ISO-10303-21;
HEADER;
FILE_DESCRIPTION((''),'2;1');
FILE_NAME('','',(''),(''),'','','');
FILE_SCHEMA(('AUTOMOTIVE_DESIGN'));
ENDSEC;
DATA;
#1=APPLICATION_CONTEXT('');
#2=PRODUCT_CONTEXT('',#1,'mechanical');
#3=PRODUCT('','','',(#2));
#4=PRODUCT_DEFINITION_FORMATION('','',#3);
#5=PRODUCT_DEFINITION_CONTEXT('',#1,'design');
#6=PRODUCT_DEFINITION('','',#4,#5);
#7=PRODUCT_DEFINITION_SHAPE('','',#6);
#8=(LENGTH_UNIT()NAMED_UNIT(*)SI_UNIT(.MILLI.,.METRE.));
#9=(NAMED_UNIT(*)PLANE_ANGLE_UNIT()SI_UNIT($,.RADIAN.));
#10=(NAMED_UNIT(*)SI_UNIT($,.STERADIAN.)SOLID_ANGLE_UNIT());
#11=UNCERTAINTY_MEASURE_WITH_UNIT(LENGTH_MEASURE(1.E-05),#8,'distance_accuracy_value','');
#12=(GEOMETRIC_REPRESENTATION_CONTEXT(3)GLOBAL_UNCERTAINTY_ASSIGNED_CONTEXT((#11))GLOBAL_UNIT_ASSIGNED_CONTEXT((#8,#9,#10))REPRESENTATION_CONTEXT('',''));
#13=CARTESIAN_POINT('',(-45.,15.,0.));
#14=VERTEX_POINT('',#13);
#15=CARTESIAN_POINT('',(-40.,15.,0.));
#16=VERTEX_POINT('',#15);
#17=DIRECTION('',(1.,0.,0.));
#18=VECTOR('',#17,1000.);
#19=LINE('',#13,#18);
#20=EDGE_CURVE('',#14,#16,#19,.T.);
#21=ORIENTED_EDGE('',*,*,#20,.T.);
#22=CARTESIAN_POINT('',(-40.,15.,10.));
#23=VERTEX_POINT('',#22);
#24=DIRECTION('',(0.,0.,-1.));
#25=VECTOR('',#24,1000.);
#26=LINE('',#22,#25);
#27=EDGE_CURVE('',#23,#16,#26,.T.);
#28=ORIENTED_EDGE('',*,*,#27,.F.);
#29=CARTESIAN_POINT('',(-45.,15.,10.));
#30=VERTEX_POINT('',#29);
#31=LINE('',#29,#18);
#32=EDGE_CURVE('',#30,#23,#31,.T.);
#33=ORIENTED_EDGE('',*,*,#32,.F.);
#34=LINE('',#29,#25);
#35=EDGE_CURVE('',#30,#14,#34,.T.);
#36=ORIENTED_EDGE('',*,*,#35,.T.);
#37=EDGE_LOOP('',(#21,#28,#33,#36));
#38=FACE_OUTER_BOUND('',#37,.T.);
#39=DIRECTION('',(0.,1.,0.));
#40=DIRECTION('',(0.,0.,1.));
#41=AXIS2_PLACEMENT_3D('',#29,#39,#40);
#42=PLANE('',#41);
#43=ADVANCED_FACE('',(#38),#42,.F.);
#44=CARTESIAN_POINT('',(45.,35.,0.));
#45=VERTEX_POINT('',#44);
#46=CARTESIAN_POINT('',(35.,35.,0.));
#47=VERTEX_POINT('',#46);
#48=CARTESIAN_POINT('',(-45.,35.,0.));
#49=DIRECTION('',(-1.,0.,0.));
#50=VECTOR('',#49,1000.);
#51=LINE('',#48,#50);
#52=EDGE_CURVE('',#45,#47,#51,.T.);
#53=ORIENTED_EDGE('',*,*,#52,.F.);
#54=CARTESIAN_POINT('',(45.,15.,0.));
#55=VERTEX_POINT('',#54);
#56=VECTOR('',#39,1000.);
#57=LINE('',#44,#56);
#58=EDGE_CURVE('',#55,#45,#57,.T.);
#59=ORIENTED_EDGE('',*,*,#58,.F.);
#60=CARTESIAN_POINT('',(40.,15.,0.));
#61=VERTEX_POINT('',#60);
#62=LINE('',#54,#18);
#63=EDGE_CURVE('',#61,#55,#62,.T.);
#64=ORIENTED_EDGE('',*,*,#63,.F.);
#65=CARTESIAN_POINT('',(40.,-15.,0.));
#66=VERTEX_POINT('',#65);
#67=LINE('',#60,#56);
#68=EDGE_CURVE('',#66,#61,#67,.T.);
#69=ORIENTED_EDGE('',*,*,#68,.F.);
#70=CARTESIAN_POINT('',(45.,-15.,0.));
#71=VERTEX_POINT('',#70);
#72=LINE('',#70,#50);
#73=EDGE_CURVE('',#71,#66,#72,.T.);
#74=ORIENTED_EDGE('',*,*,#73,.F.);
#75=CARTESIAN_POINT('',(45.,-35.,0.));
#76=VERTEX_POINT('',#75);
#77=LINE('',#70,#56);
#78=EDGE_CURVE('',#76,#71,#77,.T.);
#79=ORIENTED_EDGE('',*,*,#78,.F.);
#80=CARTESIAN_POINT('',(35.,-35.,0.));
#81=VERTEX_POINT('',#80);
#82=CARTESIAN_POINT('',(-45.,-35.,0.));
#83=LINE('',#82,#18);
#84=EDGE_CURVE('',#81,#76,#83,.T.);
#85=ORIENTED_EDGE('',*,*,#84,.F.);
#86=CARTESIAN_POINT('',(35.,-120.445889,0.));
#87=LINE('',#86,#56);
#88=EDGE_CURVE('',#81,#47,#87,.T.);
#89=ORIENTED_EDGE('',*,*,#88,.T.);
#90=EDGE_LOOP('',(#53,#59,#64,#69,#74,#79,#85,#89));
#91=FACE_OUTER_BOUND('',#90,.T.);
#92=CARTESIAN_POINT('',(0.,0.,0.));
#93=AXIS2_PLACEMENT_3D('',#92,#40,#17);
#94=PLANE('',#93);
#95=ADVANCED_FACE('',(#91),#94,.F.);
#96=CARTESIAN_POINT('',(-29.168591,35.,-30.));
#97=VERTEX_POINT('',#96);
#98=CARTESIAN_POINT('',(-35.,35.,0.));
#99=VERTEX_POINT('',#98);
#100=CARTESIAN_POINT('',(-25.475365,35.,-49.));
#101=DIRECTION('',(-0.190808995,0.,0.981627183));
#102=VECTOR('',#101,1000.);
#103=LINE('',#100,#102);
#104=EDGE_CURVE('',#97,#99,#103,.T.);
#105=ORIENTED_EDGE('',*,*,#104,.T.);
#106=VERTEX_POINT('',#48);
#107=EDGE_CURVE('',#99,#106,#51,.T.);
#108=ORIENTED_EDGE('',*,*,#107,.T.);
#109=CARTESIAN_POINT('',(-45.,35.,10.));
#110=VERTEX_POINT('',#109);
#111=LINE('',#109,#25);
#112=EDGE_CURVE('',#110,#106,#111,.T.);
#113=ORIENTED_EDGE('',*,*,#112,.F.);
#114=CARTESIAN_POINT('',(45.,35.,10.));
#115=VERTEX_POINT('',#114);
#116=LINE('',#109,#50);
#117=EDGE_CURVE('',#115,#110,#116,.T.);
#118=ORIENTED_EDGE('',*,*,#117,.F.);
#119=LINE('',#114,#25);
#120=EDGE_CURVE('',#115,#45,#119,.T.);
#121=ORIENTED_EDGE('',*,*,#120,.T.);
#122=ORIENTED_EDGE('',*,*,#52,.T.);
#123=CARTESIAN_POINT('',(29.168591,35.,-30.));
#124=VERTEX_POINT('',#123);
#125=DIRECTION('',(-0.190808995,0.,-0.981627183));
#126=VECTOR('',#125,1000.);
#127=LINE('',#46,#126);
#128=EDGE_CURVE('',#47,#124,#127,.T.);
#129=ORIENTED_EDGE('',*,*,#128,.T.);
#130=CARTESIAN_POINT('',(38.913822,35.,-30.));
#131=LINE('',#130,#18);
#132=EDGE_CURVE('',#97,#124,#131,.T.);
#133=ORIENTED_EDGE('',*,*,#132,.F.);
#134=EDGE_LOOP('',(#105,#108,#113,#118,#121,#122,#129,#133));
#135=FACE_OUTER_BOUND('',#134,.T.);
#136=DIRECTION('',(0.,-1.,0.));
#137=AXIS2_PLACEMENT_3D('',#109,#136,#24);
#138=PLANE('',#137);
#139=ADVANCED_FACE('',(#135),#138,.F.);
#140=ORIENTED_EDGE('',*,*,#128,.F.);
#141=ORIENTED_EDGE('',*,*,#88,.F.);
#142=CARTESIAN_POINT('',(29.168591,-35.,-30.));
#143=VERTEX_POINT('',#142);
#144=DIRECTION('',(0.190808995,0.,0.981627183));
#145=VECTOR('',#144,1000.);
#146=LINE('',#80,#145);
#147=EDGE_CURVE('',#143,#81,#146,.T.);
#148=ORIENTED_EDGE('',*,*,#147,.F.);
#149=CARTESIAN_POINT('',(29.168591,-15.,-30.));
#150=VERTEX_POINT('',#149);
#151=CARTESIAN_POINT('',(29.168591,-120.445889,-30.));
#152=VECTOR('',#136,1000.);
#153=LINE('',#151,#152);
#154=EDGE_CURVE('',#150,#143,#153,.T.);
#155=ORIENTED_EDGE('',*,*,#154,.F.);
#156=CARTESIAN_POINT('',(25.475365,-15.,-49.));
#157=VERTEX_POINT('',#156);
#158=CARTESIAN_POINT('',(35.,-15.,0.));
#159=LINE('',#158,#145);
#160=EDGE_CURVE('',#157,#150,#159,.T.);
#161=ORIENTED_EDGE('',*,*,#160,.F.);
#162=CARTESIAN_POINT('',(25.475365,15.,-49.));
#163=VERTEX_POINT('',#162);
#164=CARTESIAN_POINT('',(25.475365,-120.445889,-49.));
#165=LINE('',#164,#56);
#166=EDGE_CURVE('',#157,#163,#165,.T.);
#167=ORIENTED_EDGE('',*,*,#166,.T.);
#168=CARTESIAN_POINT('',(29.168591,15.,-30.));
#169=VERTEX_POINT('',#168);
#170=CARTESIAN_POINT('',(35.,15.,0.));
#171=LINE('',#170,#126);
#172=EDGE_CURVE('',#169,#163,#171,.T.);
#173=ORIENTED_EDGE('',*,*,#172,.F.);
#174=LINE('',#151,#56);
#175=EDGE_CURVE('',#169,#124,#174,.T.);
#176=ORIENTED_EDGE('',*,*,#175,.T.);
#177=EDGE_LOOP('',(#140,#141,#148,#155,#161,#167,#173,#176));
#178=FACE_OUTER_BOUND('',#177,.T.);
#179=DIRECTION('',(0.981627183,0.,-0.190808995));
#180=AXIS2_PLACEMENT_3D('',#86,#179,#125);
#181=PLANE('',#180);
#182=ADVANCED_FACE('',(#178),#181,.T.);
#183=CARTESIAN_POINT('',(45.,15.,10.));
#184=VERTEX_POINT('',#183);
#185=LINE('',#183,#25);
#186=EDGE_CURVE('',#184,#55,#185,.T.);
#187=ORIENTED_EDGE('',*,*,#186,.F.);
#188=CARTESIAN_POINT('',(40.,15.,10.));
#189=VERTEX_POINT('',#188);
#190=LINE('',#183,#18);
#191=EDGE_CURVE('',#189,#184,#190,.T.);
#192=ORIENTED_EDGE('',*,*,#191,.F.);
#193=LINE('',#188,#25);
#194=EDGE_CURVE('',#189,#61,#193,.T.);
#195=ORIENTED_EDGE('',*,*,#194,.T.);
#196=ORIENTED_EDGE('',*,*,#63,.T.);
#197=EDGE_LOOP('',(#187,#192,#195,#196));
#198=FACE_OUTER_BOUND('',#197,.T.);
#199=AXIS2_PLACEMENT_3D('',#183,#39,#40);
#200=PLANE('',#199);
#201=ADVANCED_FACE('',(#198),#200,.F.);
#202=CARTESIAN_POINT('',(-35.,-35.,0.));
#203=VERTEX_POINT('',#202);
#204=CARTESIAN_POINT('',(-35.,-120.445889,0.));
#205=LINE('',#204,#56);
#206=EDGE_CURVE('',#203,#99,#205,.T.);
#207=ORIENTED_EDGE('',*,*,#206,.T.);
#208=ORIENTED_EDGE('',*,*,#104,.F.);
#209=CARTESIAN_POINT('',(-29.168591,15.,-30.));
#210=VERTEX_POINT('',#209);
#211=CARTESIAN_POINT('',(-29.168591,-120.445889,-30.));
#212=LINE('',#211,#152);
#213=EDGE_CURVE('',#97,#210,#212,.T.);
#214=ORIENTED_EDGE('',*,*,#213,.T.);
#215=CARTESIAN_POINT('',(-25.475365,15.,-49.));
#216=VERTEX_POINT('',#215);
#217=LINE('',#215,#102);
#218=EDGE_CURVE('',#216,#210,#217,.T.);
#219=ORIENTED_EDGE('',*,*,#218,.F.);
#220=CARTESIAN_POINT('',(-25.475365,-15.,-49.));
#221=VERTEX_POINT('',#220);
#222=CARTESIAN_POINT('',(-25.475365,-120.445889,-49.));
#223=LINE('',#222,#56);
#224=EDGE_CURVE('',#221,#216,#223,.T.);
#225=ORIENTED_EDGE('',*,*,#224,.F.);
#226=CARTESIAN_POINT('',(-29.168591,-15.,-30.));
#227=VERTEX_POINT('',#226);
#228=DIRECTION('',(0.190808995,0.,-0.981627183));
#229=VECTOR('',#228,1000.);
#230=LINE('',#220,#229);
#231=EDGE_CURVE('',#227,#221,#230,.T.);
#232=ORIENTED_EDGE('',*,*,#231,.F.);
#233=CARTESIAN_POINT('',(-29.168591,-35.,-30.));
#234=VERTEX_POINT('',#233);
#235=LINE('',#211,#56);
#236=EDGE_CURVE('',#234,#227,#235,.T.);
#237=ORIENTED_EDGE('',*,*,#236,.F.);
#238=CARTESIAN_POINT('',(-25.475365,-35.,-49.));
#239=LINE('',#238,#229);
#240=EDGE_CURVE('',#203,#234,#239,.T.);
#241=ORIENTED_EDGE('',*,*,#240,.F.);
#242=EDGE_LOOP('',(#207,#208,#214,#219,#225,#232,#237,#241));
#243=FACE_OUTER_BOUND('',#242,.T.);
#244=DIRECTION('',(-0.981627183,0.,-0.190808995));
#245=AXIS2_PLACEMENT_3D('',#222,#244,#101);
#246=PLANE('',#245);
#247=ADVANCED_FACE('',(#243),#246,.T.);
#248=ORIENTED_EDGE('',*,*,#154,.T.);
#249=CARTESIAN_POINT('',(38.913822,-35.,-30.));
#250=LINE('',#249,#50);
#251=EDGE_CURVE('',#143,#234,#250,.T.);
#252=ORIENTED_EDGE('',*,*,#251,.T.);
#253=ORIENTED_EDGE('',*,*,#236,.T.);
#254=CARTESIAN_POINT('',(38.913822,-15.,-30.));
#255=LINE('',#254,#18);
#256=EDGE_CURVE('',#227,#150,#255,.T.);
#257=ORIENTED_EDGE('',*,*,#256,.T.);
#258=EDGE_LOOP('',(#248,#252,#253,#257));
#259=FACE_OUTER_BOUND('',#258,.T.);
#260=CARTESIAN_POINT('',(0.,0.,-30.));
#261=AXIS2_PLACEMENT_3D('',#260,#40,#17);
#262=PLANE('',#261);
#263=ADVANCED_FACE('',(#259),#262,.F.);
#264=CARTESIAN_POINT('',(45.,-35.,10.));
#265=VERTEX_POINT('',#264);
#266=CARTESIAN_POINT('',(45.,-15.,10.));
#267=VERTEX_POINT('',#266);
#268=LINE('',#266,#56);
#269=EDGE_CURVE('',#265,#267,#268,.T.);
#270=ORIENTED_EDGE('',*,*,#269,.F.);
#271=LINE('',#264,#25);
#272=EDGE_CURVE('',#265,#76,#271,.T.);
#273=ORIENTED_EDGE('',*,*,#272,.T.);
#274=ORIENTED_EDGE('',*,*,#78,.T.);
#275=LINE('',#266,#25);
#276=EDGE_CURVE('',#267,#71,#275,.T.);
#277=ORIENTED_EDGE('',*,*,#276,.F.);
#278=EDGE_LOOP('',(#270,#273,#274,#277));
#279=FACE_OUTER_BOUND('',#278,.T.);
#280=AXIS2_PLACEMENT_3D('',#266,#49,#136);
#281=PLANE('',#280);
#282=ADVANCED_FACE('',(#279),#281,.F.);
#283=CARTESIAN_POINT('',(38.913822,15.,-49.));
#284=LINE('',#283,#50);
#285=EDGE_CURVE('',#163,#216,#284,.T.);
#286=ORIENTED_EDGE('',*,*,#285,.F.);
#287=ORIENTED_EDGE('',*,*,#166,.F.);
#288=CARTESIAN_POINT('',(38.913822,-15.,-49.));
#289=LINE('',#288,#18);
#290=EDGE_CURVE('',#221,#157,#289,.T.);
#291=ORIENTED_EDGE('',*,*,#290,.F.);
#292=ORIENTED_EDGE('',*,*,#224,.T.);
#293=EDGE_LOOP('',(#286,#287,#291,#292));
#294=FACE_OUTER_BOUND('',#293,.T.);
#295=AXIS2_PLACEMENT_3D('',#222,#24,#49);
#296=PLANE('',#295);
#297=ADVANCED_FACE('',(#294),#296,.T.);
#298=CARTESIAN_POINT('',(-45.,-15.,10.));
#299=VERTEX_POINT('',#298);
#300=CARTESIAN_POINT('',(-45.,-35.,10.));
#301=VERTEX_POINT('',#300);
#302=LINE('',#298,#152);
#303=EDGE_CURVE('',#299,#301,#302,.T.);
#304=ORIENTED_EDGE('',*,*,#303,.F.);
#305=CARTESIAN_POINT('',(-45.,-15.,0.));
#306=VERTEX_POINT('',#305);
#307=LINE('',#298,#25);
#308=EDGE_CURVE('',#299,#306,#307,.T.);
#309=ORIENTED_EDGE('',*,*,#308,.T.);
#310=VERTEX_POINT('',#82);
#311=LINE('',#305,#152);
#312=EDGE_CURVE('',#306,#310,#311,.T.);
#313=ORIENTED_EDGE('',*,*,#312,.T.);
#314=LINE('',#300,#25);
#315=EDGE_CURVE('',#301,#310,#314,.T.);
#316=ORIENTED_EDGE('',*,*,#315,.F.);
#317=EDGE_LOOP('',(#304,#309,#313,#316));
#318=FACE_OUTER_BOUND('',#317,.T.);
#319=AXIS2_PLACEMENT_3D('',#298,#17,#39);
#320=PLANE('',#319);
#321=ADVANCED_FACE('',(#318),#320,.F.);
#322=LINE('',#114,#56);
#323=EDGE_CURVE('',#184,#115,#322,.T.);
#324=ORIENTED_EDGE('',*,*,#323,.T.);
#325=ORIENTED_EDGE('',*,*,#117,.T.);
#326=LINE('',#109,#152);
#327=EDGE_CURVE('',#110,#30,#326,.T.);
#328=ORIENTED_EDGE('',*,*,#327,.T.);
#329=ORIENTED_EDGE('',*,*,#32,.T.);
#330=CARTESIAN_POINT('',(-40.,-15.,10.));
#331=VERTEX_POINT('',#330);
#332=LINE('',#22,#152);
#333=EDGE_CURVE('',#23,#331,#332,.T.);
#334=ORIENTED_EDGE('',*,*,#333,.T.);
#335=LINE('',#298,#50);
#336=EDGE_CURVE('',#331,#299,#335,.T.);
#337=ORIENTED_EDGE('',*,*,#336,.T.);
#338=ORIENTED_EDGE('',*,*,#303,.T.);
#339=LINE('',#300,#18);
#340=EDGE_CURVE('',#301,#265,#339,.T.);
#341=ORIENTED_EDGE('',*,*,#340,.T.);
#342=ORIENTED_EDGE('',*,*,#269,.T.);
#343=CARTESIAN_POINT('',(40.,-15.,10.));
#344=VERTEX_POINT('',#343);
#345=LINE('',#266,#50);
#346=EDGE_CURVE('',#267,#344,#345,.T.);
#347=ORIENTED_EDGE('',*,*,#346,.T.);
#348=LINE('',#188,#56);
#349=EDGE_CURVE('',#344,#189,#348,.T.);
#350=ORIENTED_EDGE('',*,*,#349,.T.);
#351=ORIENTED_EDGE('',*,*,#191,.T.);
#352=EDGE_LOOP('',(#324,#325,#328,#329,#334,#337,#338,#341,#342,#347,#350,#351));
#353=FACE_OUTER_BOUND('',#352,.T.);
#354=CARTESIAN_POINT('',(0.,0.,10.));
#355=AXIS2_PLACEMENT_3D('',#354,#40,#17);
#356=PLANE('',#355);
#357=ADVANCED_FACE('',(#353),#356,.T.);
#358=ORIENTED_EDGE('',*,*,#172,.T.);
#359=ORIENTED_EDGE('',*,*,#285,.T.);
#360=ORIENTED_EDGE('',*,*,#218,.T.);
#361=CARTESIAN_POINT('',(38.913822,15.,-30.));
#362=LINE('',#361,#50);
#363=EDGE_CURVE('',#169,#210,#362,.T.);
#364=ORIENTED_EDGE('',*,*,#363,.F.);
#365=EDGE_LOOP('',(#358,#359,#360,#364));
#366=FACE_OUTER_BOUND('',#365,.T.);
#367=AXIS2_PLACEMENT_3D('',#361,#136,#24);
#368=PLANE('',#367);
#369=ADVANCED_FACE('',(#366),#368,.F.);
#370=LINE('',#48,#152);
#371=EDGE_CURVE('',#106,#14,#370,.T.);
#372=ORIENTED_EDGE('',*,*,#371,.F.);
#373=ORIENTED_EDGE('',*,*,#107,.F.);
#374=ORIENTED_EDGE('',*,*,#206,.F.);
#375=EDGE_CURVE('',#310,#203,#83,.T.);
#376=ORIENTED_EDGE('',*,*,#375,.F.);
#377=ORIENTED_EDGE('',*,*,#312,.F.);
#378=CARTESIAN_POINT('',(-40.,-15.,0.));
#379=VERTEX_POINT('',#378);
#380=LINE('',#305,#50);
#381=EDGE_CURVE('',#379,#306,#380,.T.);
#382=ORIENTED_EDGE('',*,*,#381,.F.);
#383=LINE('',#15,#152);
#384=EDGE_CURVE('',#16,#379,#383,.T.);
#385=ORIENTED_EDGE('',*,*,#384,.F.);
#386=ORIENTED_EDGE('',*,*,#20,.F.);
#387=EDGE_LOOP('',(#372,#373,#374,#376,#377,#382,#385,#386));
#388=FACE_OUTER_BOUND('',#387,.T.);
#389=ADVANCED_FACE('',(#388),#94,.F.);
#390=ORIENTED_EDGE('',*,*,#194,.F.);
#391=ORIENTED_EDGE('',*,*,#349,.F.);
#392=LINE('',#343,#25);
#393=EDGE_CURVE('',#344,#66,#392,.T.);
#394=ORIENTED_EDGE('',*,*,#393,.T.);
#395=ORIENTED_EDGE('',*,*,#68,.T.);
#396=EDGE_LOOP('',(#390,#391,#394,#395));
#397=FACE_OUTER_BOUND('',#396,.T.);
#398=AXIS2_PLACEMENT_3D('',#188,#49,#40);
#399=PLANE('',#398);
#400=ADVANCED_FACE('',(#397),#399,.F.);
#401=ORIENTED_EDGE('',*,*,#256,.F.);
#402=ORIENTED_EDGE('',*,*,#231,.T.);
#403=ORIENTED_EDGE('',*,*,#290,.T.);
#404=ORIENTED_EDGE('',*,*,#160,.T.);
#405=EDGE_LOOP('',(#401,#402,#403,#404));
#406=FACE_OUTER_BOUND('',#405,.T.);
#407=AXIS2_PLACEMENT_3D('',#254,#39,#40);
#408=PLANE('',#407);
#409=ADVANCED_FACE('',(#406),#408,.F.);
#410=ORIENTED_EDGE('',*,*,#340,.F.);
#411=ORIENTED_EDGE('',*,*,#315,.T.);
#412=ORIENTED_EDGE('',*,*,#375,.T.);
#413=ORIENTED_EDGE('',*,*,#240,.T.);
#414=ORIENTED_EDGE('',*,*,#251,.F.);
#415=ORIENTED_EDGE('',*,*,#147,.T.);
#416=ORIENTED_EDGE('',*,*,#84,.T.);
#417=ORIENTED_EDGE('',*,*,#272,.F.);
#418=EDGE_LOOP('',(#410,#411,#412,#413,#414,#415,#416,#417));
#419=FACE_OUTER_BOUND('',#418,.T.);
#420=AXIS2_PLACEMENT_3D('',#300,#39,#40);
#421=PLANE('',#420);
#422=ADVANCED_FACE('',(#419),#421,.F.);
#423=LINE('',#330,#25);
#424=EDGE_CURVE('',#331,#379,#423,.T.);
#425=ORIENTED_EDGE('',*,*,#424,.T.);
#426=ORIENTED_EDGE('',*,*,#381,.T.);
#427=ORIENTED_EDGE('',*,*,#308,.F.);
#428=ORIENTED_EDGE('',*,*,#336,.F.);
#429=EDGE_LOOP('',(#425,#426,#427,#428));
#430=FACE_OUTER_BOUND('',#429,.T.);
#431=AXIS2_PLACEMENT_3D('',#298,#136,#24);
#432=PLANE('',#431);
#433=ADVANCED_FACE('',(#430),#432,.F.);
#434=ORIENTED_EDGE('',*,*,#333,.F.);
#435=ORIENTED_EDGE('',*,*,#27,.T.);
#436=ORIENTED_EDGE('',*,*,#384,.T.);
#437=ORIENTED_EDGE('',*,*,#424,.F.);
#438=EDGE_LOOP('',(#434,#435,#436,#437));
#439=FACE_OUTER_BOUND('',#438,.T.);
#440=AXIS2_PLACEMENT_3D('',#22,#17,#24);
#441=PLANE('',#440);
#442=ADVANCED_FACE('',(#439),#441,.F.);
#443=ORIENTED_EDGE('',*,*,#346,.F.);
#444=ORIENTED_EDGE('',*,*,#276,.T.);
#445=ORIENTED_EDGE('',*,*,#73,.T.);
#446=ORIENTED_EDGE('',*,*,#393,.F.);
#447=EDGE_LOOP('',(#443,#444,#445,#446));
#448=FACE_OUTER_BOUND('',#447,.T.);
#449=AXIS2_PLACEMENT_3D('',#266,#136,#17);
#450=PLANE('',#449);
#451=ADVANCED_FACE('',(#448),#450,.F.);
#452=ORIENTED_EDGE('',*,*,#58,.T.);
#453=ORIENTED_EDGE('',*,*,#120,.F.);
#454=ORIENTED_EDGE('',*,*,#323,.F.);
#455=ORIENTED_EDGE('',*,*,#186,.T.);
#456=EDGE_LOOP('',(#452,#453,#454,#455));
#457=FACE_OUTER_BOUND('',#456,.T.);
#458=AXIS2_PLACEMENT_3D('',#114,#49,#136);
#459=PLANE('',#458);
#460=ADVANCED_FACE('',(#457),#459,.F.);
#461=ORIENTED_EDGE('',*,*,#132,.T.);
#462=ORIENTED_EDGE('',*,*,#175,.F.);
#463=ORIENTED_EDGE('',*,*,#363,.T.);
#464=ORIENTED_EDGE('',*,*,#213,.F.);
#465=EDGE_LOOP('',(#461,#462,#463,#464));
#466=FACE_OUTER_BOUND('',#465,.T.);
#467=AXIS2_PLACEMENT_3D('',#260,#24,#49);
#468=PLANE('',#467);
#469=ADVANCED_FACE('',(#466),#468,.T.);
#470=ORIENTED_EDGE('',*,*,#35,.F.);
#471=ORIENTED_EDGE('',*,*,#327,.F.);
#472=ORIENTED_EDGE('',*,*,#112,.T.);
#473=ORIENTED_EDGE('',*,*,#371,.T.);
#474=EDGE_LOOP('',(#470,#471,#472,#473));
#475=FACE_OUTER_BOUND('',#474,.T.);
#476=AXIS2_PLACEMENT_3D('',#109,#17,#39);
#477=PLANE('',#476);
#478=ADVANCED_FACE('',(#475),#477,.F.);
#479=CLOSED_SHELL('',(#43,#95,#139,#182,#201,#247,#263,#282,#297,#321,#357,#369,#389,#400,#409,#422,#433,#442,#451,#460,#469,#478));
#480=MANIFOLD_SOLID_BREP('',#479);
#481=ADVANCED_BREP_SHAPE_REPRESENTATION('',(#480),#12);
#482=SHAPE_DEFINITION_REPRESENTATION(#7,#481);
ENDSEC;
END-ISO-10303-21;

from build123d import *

# Parameters (mm, degrees)
BASE_PLATE_DEPTH        = 10
TAPERED_BOSS_DEPTH      = 70
TOP_SLOT_PROFILE_W      = 92.427210419
TOP_SLOT_PROFILE_H      = 20
TOP_SLOT_PROFILE_W_2    = 89.987361697
TOP_SLOT_CUT_19MM_DEPTH = 19


with BuildPart() as part:
    # Base Plate Profile → Base Plate (new body)
    with BuildSketch(Plane.XY):
        Polygon((-45, -15), (-45, -35), (45, -35), (45, -15), (40, -15), (40, 15), (45, 15), (45, 35), (-45, 35), (-45, 15), (-40, 15), (-40, -15), align=None)
    extrude(amount=BASE_PLATE_DEPTH)

    # Tapered Boss Profile → Tapered Boss (add)
    with BuildSketch(Plane(origin=(0, 35, 0), x_dir=(1, 0, 0), z_dir=(0, 1, 0))):
        Polygon((-25.475364852, 49), (-35, 0), (35, 0), (25.475364852, 49), align=None)
    extrude(amount=-TAPERED_BOSS_DEPTH)

    # Top Slot Profile → Top Slot Cut 19mm (cut)
    with BuildSketch(Plane(origin=(0, 0, -49), x_dir=(-1, 0, 0), z_dir=(0, 0, -1))):
        with Locations((7.299783504, 25)):
            Rectangle(TOP_SLOT_PROFILE_W, TOP_SLOT_PROFILE_H)
        with Locations((6.079859143, -25)):
            Rectangle(TOP_SLOT_PROFILE_W_2, TOP_SLOT_PROFILE_H)
    extrude(amount=-TOP_SLOT_CUT_19MM_DEPTH, mode=Mode.SUBTRACT)


solid = part.part
